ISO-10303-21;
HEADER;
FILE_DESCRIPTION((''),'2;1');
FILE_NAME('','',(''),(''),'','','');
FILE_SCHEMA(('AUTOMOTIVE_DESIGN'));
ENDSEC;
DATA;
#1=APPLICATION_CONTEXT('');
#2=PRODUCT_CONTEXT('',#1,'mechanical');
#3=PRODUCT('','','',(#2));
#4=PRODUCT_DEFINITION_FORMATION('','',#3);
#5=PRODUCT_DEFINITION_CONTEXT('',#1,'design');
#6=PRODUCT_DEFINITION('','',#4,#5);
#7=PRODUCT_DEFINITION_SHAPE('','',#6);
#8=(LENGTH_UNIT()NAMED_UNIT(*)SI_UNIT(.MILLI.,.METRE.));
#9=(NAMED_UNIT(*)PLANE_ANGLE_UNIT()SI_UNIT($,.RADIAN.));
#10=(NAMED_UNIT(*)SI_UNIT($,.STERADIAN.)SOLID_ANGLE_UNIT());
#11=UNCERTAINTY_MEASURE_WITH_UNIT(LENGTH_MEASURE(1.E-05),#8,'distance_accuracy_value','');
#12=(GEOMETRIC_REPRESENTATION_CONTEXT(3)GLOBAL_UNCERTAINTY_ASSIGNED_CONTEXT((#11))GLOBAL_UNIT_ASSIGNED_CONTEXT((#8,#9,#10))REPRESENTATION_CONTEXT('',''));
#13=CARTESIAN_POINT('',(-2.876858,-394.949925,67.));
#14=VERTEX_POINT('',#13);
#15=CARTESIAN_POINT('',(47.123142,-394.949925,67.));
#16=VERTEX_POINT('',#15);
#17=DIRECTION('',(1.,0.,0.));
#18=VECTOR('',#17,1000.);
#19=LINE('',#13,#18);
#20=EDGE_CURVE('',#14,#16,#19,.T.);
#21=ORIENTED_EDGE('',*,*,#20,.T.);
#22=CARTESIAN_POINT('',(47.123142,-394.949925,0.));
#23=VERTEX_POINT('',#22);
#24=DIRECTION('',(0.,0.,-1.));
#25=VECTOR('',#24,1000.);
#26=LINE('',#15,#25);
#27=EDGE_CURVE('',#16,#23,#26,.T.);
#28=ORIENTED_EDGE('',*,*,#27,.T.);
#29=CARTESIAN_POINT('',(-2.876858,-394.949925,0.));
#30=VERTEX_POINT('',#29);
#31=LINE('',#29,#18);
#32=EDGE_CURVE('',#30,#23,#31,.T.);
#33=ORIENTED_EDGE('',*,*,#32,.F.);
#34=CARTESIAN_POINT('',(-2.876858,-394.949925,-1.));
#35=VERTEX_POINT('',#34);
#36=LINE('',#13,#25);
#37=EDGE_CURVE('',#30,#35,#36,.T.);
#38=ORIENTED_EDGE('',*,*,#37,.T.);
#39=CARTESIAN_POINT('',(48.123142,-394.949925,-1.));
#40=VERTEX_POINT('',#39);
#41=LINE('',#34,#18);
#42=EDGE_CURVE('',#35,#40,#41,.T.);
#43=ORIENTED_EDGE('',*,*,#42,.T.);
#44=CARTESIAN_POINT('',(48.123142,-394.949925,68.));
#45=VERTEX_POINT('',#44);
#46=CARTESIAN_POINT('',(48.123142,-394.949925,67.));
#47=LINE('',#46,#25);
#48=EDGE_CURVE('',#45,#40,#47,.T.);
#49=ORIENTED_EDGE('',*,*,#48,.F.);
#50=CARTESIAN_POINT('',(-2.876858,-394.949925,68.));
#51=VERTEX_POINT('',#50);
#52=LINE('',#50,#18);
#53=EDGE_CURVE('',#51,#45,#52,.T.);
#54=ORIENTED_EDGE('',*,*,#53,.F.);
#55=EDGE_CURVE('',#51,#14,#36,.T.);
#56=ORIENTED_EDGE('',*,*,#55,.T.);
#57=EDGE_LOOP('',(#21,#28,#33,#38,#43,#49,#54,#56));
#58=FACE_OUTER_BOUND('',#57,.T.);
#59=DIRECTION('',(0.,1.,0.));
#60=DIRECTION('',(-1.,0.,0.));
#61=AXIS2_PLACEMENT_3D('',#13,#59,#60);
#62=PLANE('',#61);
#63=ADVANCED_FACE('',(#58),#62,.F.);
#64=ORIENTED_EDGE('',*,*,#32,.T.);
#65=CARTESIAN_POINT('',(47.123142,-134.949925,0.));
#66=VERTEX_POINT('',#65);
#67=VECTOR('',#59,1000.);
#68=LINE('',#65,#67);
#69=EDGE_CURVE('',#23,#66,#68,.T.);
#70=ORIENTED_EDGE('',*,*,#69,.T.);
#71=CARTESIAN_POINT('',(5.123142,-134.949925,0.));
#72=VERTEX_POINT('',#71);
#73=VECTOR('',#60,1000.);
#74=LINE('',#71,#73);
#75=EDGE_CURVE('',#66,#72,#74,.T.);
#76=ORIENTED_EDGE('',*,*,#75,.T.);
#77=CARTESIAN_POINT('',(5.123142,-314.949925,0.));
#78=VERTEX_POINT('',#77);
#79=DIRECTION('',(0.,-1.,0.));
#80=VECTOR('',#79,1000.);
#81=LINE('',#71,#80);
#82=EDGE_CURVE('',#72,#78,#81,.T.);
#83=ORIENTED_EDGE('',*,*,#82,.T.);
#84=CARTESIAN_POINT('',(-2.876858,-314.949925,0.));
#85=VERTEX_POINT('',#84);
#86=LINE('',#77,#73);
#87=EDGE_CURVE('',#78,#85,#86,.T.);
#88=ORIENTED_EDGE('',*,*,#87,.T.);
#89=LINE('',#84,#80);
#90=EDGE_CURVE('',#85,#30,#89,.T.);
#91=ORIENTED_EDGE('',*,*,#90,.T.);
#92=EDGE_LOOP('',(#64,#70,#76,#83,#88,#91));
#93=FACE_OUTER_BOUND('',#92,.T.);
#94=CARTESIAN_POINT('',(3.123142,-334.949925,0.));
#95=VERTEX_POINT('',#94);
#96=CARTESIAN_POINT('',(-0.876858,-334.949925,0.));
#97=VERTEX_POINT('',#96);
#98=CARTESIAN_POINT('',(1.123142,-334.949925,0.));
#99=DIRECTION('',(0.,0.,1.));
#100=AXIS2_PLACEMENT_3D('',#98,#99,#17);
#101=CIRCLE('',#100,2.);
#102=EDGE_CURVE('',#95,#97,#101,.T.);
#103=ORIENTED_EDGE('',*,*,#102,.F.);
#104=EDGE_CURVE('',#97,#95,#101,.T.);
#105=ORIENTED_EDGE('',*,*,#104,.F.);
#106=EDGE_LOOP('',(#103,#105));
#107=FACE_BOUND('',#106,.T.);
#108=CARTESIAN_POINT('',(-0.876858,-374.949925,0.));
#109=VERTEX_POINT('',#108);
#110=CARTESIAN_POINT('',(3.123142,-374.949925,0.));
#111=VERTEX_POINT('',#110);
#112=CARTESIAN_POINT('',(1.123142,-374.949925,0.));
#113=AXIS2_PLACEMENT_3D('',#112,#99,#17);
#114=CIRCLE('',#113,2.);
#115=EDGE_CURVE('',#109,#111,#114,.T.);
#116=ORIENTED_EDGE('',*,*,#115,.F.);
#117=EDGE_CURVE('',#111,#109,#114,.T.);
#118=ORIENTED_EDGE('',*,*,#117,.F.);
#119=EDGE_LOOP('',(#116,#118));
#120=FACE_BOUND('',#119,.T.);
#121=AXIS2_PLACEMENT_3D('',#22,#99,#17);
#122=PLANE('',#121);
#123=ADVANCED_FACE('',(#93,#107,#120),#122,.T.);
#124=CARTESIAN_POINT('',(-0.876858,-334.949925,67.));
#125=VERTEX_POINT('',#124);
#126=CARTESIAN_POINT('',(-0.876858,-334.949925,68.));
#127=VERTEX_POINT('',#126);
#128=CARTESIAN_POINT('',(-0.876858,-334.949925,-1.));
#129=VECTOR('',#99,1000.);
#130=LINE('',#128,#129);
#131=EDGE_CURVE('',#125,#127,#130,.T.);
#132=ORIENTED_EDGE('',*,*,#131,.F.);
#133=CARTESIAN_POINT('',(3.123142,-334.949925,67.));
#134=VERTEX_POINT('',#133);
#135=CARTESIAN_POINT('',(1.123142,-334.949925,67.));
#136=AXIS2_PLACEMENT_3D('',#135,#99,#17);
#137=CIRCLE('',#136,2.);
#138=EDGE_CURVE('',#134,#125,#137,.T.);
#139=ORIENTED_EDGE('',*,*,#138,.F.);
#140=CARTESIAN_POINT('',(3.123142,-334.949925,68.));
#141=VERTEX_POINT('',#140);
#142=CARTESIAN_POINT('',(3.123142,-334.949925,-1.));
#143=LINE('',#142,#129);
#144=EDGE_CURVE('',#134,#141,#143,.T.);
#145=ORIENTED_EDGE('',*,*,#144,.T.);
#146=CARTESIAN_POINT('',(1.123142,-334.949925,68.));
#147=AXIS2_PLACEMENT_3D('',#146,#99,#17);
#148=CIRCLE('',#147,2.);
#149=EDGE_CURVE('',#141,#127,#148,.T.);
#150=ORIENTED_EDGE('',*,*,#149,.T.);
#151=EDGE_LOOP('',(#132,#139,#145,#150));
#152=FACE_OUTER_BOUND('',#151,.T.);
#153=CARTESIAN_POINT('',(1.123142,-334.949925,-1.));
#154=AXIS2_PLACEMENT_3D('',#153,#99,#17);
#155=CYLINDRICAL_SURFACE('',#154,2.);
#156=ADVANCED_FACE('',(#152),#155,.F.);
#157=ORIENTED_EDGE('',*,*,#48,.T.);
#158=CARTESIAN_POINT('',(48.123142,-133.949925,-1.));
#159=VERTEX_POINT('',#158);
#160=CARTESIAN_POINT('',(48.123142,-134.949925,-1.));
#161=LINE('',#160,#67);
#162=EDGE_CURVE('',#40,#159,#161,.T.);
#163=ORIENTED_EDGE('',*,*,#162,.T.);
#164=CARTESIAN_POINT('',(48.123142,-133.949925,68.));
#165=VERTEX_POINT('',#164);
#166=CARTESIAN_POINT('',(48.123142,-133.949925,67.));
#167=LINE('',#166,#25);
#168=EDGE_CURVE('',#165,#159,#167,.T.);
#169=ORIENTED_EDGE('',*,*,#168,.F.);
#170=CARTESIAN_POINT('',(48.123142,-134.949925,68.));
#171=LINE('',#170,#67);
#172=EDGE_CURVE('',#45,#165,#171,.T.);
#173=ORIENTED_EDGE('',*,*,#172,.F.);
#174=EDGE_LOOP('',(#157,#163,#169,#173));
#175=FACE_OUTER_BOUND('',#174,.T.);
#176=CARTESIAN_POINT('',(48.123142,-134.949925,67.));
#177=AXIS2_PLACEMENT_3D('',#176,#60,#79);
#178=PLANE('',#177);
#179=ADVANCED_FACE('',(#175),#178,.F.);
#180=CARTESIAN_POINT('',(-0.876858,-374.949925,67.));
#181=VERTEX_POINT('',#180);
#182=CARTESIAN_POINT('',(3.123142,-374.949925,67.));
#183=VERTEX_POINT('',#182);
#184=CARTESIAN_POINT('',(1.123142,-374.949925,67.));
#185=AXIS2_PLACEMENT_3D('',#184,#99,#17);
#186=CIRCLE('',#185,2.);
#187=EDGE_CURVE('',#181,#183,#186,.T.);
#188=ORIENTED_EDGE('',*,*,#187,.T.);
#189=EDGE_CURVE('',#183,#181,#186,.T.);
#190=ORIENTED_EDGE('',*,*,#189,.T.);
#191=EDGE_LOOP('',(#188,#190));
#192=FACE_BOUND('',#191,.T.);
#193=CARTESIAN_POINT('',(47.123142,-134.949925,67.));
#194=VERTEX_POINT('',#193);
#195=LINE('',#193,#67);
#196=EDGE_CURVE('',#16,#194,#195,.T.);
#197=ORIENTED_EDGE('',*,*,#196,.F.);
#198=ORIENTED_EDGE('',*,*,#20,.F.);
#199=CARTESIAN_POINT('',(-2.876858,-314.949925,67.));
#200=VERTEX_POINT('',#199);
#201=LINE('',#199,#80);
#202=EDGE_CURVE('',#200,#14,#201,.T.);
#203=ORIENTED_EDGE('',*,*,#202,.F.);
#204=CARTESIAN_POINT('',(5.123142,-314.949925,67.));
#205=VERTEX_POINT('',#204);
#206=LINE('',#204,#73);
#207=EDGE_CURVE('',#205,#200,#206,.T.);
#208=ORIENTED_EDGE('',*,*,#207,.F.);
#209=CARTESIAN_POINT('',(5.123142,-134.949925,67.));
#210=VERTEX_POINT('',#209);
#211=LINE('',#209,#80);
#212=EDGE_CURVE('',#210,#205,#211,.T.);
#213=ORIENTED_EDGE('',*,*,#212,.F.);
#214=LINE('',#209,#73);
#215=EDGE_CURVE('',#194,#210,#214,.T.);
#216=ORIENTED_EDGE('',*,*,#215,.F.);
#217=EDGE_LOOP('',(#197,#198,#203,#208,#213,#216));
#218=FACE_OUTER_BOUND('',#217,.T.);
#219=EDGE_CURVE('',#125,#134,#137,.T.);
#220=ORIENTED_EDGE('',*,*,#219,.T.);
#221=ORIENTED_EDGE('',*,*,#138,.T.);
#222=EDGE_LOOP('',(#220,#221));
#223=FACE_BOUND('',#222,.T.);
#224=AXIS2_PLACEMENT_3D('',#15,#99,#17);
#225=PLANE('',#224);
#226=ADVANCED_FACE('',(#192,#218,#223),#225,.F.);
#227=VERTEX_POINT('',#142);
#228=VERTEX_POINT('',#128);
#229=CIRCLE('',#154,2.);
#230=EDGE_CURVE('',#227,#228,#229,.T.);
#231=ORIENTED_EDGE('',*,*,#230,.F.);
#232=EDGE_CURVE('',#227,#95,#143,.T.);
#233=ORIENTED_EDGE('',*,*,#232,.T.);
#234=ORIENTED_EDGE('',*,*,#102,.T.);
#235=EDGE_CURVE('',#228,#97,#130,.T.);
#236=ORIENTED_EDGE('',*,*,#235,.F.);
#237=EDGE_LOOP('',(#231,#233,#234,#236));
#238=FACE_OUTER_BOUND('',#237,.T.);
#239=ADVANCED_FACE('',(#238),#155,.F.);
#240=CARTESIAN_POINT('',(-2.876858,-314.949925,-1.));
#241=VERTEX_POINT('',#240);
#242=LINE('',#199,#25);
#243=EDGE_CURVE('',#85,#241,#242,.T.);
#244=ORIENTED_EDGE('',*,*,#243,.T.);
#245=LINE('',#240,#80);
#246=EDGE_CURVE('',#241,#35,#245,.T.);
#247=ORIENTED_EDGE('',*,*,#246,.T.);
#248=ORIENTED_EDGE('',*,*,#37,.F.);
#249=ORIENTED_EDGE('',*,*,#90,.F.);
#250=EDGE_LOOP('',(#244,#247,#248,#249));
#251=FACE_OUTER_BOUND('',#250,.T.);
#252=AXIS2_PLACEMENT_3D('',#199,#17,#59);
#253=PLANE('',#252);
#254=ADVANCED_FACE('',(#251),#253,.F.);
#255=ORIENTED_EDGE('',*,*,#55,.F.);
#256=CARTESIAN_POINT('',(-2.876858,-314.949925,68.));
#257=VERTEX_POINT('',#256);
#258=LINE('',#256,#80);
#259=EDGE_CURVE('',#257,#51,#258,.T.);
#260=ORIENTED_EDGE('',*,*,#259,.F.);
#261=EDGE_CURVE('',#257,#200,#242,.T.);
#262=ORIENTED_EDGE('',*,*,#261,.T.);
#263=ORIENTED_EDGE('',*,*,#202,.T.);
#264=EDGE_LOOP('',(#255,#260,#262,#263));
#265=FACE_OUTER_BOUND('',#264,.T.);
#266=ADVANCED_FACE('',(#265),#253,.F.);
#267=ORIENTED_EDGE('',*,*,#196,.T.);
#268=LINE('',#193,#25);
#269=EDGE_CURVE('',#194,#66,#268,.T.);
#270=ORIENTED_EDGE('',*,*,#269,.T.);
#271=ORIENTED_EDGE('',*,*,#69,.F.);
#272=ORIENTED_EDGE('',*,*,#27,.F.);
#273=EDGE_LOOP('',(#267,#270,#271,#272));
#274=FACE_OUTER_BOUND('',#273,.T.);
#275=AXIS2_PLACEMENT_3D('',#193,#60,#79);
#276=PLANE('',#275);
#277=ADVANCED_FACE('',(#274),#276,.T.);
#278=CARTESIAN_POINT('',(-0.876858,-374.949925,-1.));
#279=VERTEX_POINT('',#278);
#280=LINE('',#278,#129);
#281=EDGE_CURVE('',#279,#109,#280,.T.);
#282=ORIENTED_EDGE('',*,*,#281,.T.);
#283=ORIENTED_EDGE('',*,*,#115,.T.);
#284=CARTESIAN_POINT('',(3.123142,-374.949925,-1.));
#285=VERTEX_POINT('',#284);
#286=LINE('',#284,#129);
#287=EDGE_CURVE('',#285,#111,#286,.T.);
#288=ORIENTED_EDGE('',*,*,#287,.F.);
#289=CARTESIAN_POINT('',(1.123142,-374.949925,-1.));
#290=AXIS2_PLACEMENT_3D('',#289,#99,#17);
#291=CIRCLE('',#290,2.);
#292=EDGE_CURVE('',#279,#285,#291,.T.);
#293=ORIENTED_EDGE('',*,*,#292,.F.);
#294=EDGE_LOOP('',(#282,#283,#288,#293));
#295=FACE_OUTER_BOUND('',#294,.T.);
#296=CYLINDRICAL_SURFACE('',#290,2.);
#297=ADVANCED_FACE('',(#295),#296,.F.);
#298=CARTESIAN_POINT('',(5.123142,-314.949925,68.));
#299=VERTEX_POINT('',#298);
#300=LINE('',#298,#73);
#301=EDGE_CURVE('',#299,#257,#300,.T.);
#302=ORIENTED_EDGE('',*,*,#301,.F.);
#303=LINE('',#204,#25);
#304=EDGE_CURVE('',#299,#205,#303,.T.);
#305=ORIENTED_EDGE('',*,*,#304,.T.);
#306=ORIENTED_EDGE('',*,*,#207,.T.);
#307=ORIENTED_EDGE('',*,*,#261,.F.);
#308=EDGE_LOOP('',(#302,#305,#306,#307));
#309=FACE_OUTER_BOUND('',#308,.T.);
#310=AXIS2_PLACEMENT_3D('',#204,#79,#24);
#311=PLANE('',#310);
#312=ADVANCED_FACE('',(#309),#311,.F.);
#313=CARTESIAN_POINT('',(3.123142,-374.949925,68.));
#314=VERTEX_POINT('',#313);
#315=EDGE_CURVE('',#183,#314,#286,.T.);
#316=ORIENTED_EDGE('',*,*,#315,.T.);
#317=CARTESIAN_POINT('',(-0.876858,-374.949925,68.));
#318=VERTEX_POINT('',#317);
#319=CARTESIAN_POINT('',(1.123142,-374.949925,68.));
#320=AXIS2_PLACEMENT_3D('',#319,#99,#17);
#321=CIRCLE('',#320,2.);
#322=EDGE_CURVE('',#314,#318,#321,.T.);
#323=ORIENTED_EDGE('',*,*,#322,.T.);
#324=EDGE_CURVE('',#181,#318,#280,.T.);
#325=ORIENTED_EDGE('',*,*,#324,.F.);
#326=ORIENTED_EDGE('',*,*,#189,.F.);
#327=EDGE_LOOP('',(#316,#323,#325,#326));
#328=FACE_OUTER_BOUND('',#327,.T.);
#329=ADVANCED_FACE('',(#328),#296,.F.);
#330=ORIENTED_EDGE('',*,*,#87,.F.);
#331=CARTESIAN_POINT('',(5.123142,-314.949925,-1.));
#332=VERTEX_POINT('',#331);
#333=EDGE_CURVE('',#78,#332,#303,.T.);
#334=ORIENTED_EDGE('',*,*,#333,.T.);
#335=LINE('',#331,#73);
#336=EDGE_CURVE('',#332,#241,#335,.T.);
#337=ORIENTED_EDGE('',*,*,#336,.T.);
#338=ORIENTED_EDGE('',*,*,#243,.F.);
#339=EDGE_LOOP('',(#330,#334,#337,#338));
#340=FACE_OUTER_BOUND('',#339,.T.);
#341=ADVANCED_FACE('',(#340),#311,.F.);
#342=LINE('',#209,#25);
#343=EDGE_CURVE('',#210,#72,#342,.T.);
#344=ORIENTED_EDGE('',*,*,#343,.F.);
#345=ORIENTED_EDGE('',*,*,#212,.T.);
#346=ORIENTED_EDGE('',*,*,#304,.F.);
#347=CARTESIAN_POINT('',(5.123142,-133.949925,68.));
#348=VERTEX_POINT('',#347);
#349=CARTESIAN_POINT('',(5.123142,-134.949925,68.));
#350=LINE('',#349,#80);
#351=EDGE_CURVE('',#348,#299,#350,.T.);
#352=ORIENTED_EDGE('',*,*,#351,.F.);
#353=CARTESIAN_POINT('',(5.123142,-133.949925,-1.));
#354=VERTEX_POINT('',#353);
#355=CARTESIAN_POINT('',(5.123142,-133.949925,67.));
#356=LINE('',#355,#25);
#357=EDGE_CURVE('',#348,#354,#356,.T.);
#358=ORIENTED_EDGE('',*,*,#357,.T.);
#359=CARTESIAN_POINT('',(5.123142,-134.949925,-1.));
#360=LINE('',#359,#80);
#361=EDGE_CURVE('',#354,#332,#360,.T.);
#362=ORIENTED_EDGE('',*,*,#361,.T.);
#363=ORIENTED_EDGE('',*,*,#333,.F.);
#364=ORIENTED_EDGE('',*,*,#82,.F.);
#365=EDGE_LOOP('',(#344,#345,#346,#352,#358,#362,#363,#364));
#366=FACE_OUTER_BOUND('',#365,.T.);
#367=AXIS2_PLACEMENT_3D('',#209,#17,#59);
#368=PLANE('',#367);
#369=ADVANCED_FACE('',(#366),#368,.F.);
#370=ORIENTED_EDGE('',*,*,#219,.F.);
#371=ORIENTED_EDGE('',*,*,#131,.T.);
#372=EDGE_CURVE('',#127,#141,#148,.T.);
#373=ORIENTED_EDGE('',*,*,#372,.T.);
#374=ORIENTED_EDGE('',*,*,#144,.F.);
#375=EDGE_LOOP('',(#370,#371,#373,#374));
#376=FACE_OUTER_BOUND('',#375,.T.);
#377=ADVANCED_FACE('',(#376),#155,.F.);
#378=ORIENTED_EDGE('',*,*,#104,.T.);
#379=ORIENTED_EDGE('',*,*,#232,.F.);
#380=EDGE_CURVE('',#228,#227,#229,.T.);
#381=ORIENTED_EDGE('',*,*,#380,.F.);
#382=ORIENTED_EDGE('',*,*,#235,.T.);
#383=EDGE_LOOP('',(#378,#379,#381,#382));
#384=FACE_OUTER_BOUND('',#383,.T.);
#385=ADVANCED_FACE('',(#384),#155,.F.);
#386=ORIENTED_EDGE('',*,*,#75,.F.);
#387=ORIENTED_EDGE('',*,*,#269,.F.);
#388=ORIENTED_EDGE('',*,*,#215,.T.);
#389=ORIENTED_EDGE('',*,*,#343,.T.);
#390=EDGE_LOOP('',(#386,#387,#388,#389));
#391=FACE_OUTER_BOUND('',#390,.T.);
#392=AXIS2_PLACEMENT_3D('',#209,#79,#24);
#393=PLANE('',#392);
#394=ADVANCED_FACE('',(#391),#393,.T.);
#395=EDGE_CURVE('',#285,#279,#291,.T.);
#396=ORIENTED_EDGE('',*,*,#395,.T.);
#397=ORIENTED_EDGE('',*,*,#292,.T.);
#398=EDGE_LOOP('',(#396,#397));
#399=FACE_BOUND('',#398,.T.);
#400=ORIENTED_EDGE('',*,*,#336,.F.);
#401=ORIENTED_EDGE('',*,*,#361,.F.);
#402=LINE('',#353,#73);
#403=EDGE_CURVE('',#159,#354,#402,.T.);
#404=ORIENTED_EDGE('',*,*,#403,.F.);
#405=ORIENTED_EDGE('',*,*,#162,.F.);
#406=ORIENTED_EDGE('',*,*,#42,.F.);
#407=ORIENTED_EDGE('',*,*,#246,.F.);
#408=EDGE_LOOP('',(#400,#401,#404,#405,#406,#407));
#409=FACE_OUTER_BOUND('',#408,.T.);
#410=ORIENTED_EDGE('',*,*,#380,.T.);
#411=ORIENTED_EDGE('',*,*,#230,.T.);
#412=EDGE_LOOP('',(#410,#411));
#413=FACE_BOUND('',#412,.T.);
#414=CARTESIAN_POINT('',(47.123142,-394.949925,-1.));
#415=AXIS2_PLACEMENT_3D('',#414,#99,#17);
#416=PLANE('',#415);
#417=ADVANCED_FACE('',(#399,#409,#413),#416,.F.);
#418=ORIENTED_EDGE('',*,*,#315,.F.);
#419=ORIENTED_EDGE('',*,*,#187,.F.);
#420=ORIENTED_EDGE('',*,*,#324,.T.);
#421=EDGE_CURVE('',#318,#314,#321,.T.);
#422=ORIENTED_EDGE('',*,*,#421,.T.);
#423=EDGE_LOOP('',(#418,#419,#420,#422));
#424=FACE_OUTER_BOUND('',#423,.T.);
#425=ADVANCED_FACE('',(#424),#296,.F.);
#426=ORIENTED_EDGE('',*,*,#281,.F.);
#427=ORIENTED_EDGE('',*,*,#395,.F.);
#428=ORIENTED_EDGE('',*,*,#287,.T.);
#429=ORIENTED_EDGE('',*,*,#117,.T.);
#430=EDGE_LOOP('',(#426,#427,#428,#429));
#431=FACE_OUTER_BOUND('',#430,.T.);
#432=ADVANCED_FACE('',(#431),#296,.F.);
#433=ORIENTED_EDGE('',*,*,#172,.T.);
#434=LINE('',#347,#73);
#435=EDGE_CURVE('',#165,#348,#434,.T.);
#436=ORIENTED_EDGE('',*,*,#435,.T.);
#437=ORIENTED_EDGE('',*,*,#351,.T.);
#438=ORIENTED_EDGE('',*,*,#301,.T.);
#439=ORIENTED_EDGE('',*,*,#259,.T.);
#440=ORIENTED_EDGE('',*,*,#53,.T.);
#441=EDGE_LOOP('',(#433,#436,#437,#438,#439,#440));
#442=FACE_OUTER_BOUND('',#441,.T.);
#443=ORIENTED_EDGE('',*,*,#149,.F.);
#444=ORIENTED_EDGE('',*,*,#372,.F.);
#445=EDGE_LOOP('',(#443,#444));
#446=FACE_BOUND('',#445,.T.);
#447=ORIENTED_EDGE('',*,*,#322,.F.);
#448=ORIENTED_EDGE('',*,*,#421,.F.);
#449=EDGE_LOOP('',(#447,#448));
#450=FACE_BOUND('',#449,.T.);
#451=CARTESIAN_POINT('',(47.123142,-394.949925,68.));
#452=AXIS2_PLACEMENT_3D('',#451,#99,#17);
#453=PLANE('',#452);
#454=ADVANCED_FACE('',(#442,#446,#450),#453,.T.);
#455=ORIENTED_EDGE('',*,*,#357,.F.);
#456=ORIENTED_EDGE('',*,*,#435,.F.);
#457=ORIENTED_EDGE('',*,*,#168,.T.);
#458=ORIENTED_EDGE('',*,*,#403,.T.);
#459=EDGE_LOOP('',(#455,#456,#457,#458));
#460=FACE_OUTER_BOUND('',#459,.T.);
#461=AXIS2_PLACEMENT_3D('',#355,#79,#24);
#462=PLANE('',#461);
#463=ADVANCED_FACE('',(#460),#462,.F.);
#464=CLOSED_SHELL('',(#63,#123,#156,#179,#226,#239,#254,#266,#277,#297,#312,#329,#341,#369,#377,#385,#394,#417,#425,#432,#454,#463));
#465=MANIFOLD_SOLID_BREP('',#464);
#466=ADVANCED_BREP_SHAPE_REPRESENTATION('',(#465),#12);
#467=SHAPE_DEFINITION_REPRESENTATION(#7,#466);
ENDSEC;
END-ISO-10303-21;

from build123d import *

# Parameters (mm, degrees)
EXTRUDE_1_DEPTH        = 67
SHELL_1_T              = 1
SKETCH_2_R             = 2
CUT_EXTRUDE_1_DEPTH    = 404.809707905
PATTERN_LINEAR_1_COUNT = 2
PATTERN_LINEAR_1_PITCH = 40


with BuildPart() as part:
    # 草图1 → 凸台-拉伸1 (new body)
    with BuildSketch(Plane.XY):
        Polygon((5.123141908, -134.949925194), (5.123141908, -314.949925194), (-2.876858092, -314.949925194), (-2.876858092, -394.949925194), (47.123141908, -394.949925194), (47.123141908, -134.949925194), align=None)
    extrude(amount=EXTRUDE_1_DEPTH)

    # 抽壳1
    shell_1_openings = [part.faces().sort_by_distance(p)[0] for p in [
        (5.123141908, -224.949925194, 33.5),
        (1.123141908, -314.949925194, 33.5),
        (-2.876858092, -354.949925194, 33.5),
        (22.123141908, -394.949925194, 33.5),
    ]]
    offset(amount=SHELL_1_T, openings=shell_1_openings, kind=Kind.INTERSECTION)

    # 草图2 → 切除-拉伸1 (cut, through all)
    with BuildSketch(Plane.XY.offset(68)):
        with Locations((1.123141908, -374.949925194)):
            Circle(SKETCH_2_R)
    cut_extrude_1 = extrude(amount=-CUT_EXTRUDE_1_DEPTH, mode=Mode.SUBTRACT)

    # 阵列(线性)1: 切除-拉伸1 ×2
    with Locations(*[(0, i * PATTERN_LINEAR_1_PITCH, 0) for i in range(1, PATTERN_LINEAR_1_COUNT)]):
        add(cut_extrude_1, mode=Mode.SUBTRACT)


solid = part.part
